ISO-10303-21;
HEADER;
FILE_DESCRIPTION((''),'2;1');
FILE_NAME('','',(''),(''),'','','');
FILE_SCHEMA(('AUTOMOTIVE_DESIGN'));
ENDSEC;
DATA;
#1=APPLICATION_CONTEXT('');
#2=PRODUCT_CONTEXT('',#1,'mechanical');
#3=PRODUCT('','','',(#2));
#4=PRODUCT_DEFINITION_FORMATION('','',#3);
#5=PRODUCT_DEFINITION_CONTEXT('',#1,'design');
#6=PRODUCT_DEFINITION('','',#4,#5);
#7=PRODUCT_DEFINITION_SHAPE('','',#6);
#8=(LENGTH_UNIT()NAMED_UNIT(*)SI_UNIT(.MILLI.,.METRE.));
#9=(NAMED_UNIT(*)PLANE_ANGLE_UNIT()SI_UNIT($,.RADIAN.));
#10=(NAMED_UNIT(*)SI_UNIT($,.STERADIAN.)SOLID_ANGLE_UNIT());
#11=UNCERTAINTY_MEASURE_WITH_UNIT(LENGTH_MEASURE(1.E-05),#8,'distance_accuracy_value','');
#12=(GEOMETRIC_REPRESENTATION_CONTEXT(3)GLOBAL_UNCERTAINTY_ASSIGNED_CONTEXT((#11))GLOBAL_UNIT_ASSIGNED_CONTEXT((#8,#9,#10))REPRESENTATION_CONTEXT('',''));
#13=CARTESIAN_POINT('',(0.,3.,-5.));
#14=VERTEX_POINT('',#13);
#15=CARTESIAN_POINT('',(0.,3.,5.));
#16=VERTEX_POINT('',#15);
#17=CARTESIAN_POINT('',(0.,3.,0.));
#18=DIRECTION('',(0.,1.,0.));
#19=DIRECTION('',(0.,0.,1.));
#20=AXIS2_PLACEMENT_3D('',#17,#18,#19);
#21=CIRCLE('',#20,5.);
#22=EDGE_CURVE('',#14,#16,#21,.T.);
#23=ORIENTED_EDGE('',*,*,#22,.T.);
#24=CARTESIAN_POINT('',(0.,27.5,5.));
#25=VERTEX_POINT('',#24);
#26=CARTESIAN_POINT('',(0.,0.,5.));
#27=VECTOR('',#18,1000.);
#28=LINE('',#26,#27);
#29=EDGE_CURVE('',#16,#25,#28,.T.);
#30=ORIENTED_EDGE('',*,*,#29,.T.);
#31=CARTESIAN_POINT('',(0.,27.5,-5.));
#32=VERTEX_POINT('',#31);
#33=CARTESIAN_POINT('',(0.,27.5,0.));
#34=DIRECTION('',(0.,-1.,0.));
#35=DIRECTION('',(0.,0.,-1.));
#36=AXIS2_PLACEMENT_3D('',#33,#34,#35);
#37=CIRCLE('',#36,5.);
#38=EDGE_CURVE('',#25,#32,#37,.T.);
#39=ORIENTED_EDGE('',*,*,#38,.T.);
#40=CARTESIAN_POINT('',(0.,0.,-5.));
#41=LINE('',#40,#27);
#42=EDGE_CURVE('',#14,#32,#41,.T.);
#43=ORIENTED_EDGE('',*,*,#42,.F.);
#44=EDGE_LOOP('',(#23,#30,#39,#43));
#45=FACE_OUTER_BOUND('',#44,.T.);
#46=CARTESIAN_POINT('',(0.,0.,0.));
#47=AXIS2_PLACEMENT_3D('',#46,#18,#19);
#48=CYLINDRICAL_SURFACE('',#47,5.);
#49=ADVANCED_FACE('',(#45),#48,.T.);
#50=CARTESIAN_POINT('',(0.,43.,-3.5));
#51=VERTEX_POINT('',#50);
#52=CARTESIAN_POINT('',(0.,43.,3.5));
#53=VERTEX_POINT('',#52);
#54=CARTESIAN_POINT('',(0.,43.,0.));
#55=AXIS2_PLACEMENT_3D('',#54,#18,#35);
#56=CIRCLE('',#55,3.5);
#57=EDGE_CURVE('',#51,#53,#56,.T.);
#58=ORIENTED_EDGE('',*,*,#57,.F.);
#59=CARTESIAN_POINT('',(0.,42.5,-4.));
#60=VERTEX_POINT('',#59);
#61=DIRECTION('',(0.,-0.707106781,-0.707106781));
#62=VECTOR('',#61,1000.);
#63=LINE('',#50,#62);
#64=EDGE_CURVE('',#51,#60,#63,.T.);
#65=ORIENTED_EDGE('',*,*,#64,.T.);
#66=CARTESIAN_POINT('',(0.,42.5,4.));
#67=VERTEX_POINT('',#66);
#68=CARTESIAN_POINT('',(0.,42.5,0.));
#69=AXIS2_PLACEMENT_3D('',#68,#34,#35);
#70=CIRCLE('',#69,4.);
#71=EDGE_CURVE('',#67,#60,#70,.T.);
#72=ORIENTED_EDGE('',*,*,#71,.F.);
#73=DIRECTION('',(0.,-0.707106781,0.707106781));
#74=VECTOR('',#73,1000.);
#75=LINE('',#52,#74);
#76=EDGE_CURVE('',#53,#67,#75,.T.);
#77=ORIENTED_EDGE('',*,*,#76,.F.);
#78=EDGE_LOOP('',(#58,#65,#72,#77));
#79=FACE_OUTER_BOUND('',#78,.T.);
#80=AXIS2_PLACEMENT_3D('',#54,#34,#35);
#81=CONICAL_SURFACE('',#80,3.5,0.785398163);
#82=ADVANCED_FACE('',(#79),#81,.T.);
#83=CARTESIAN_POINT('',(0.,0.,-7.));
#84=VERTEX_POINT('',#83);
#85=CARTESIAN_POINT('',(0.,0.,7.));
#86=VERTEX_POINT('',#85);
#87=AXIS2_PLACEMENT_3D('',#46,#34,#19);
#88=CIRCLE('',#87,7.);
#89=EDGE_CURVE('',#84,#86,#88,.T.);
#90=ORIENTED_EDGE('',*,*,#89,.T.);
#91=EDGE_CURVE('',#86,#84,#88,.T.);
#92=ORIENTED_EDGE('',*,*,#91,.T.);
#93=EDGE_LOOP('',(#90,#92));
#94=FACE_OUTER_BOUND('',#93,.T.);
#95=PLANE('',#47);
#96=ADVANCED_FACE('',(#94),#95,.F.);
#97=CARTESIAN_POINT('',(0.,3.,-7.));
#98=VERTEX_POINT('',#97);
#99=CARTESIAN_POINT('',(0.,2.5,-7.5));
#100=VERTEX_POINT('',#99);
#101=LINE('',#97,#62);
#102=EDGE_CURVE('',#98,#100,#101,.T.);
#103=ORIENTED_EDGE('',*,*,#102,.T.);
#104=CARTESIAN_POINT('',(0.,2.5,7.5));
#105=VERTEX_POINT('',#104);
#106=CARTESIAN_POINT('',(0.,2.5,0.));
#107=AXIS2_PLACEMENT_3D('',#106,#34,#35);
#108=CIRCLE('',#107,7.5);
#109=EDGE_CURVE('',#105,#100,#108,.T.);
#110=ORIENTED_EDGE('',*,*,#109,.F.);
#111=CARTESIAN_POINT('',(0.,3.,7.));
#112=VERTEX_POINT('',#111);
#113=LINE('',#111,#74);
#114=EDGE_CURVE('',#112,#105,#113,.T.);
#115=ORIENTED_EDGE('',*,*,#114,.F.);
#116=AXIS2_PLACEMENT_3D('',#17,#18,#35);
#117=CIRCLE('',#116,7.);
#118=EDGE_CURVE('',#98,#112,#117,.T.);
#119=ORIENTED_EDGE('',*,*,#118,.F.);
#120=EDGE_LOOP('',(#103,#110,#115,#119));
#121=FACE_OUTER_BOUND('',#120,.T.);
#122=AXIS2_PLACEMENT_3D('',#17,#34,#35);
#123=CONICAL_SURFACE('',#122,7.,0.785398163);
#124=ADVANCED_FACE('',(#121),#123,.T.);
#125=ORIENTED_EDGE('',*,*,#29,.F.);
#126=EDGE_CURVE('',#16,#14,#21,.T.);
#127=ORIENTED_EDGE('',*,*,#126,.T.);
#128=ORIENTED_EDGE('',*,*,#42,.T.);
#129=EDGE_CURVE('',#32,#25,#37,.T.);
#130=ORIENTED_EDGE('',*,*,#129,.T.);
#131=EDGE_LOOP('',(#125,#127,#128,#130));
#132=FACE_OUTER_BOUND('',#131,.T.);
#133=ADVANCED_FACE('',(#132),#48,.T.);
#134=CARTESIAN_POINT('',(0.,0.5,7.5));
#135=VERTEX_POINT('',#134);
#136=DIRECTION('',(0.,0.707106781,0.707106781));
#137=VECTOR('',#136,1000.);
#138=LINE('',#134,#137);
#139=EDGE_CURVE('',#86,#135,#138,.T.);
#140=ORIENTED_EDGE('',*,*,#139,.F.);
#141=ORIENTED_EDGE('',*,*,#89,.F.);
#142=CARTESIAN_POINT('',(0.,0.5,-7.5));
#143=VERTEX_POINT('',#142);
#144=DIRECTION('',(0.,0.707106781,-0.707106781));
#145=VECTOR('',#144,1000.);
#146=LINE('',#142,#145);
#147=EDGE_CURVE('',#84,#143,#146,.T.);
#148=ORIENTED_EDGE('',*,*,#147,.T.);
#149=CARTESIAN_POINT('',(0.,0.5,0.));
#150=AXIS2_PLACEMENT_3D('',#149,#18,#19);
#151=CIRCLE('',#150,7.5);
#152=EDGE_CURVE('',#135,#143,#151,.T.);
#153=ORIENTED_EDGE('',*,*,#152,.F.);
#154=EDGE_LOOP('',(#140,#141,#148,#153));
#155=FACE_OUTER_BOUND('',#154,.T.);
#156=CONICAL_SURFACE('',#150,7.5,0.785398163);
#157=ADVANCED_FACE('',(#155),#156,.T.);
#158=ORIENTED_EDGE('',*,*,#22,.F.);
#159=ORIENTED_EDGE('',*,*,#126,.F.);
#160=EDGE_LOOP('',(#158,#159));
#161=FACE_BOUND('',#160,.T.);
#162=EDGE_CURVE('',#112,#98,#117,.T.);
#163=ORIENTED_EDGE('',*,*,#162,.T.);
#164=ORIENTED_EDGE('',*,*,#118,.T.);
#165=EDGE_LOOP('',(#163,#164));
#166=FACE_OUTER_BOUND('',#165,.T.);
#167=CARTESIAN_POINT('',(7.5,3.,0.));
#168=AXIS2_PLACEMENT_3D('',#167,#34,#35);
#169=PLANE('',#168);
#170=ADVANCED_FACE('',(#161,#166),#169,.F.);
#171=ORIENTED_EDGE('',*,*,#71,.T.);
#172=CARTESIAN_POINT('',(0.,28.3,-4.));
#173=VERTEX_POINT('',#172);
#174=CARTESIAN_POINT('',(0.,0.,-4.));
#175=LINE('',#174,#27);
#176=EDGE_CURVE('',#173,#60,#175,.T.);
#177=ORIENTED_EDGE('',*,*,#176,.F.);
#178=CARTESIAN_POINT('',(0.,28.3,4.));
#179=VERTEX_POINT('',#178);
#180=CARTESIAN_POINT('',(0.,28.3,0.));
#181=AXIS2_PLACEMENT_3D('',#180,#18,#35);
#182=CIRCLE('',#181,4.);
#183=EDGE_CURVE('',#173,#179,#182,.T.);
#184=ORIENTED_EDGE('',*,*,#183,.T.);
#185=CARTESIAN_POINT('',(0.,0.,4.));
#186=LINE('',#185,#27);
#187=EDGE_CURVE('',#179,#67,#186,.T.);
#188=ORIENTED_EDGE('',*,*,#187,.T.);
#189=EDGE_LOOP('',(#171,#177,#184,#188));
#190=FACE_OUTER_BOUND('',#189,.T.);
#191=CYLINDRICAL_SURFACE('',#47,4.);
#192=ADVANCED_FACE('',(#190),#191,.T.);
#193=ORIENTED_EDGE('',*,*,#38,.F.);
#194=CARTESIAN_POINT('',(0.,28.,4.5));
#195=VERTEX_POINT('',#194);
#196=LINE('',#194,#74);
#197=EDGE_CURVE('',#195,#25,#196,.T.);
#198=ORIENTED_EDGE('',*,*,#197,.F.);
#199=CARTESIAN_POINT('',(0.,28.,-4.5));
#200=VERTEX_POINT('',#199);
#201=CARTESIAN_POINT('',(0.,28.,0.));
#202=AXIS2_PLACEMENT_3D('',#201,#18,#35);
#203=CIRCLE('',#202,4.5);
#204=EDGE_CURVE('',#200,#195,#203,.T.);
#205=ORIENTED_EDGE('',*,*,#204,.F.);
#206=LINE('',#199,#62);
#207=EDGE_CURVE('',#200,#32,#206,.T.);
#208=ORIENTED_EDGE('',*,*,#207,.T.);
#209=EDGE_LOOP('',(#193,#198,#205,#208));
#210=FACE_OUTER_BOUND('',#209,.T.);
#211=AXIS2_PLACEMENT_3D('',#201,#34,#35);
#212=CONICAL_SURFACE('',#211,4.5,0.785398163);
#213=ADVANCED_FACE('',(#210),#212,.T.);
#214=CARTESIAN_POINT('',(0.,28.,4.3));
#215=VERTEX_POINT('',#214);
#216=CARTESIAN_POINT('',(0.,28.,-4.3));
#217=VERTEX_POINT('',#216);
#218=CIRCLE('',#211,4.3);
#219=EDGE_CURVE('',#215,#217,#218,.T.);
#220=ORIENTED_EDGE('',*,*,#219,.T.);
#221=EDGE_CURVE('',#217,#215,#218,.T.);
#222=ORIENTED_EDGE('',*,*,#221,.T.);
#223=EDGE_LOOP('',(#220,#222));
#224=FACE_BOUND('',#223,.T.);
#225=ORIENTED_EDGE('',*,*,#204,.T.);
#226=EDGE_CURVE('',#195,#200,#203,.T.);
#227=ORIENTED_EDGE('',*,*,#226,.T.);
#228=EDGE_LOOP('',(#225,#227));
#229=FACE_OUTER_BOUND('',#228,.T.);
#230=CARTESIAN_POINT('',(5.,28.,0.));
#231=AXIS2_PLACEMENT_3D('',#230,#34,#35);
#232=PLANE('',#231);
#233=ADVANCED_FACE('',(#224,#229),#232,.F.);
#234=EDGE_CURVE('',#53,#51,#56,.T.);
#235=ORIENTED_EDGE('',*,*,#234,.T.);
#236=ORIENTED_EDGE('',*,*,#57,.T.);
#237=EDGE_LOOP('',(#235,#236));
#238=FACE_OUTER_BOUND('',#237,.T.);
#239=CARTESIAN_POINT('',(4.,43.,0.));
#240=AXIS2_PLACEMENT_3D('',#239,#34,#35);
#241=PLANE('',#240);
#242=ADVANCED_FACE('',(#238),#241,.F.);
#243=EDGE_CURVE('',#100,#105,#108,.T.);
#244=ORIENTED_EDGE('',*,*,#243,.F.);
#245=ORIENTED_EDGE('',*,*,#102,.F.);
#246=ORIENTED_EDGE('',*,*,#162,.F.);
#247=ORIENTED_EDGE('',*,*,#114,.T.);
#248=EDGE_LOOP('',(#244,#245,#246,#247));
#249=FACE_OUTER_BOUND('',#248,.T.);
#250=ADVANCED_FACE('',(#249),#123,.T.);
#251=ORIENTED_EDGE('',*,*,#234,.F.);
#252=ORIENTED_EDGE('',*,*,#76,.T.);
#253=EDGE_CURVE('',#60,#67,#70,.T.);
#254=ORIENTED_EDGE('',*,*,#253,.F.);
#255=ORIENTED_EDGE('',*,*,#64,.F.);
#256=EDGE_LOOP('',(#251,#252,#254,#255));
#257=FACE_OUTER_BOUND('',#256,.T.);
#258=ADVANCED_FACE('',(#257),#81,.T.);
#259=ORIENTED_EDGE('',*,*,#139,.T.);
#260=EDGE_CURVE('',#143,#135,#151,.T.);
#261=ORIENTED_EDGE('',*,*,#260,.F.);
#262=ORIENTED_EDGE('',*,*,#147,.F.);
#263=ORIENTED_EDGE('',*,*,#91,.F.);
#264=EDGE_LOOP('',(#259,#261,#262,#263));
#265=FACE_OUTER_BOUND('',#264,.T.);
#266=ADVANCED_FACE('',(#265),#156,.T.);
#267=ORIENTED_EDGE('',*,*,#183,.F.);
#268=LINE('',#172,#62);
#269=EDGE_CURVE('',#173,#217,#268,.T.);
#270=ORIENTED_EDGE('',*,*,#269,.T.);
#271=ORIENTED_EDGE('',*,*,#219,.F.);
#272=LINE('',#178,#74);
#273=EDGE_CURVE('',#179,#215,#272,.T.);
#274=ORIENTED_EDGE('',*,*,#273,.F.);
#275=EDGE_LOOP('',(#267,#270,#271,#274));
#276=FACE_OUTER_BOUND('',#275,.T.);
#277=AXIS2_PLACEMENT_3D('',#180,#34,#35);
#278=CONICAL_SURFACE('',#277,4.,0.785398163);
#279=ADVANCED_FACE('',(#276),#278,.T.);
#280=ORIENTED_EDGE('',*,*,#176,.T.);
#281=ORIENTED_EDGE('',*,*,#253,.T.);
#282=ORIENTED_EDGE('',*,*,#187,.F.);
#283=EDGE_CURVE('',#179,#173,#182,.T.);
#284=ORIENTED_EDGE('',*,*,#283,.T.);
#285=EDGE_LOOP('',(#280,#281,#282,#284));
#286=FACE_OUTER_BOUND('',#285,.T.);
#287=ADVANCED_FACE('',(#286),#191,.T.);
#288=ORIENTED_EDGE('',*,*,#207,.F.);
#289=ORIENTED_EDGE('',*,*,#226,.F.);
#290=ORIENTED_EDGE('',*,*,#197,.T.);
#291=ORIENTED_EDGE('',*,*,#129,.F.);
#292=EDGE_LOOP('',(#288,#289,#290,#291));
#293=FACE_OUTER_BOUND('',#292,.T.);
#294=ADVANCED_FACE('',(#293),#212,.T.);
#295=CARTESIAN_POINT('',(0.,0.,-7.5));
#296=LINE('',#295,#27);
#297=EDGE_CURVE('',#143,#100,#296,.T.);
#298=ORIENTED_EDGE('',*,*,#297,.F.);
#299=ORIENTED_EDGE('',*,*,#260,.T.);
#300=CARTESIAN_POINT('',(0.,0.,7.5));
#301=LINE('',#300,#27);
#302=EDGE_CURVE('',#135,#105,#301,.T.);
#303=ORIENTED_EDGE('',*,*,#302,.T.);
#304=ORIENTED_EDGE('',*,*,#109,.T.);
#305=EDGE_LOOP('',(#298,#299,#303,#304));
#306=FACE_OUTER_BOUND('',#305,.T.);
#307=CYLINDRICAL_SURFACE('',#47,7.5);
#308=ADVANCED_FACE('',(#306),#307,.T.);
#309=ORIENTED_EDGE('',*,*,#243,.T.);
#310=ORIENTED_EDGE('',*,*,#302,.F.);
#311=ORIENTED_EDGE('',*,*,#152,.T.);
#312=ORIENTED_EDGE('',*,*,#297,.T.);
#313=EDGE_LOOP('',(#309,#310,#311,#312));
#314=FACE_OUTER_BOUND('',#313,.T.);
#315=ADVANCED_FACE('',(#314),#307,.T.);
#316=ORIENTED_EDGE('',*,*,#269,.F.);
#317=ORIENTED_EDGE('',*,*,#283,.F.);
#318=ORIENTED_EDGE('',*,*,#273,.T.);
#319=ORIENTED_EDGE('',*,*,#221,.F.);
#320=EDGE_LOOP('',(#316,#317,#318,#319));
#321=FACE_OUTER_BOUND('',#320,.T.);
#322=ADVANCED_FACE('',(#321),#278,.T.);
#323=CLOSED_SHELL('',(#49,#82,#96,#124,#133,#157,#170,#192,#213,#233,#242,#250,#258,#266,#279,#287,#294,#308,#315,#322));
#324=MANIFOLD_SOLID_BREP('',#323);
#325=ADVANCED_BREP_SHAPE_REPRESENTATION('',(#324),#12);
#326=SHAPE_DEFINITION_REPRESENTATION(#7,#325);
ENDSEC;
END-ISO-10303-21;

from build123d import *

# Parameters (mm, degrees)
CHAMFER1_SIZE = 0.5
CHAMFER2_SIZE = 0.3


with BuildPart() as part:
    # Sketch1 → Revolve1 (revolve)
    with BuildSketch(Plane.XY, mode=Mode.PRIVATE) as revolve1_sk:
        Polygon((0, 0), (7.5, 0), (7.5, 3), (5, 3), (5, 28), (4, 28), (4, 43), (0, 43), align=None)
    revolve(revolve1_sk.sketch.rotate(Axis((0, 0, 0), (0, -1, 0)), 90), axis=Axis((0, 0, 0), (0, -1, 0)))

    # Chamfer1
    chamfer1_edges = [part.edges().sort_by_distance(p)[0] for p in [
        (0, 43, -4),
        (0, 28, -5),
        (0, 3, -7.5),
        (0, 0, -7.5),
    ]]
    chamfer(chamfer1_edges, length=CHAMFER1_SIZE)

    # Chamfer2
    chamfer2_edges = [part.edges().sort_by_distance(p)[0] for p in [
        (0, 28, -4),
    ]]
    chamfer(chamfer2_edges, length=CHAMFER2_SIZE)


solid = part.part
